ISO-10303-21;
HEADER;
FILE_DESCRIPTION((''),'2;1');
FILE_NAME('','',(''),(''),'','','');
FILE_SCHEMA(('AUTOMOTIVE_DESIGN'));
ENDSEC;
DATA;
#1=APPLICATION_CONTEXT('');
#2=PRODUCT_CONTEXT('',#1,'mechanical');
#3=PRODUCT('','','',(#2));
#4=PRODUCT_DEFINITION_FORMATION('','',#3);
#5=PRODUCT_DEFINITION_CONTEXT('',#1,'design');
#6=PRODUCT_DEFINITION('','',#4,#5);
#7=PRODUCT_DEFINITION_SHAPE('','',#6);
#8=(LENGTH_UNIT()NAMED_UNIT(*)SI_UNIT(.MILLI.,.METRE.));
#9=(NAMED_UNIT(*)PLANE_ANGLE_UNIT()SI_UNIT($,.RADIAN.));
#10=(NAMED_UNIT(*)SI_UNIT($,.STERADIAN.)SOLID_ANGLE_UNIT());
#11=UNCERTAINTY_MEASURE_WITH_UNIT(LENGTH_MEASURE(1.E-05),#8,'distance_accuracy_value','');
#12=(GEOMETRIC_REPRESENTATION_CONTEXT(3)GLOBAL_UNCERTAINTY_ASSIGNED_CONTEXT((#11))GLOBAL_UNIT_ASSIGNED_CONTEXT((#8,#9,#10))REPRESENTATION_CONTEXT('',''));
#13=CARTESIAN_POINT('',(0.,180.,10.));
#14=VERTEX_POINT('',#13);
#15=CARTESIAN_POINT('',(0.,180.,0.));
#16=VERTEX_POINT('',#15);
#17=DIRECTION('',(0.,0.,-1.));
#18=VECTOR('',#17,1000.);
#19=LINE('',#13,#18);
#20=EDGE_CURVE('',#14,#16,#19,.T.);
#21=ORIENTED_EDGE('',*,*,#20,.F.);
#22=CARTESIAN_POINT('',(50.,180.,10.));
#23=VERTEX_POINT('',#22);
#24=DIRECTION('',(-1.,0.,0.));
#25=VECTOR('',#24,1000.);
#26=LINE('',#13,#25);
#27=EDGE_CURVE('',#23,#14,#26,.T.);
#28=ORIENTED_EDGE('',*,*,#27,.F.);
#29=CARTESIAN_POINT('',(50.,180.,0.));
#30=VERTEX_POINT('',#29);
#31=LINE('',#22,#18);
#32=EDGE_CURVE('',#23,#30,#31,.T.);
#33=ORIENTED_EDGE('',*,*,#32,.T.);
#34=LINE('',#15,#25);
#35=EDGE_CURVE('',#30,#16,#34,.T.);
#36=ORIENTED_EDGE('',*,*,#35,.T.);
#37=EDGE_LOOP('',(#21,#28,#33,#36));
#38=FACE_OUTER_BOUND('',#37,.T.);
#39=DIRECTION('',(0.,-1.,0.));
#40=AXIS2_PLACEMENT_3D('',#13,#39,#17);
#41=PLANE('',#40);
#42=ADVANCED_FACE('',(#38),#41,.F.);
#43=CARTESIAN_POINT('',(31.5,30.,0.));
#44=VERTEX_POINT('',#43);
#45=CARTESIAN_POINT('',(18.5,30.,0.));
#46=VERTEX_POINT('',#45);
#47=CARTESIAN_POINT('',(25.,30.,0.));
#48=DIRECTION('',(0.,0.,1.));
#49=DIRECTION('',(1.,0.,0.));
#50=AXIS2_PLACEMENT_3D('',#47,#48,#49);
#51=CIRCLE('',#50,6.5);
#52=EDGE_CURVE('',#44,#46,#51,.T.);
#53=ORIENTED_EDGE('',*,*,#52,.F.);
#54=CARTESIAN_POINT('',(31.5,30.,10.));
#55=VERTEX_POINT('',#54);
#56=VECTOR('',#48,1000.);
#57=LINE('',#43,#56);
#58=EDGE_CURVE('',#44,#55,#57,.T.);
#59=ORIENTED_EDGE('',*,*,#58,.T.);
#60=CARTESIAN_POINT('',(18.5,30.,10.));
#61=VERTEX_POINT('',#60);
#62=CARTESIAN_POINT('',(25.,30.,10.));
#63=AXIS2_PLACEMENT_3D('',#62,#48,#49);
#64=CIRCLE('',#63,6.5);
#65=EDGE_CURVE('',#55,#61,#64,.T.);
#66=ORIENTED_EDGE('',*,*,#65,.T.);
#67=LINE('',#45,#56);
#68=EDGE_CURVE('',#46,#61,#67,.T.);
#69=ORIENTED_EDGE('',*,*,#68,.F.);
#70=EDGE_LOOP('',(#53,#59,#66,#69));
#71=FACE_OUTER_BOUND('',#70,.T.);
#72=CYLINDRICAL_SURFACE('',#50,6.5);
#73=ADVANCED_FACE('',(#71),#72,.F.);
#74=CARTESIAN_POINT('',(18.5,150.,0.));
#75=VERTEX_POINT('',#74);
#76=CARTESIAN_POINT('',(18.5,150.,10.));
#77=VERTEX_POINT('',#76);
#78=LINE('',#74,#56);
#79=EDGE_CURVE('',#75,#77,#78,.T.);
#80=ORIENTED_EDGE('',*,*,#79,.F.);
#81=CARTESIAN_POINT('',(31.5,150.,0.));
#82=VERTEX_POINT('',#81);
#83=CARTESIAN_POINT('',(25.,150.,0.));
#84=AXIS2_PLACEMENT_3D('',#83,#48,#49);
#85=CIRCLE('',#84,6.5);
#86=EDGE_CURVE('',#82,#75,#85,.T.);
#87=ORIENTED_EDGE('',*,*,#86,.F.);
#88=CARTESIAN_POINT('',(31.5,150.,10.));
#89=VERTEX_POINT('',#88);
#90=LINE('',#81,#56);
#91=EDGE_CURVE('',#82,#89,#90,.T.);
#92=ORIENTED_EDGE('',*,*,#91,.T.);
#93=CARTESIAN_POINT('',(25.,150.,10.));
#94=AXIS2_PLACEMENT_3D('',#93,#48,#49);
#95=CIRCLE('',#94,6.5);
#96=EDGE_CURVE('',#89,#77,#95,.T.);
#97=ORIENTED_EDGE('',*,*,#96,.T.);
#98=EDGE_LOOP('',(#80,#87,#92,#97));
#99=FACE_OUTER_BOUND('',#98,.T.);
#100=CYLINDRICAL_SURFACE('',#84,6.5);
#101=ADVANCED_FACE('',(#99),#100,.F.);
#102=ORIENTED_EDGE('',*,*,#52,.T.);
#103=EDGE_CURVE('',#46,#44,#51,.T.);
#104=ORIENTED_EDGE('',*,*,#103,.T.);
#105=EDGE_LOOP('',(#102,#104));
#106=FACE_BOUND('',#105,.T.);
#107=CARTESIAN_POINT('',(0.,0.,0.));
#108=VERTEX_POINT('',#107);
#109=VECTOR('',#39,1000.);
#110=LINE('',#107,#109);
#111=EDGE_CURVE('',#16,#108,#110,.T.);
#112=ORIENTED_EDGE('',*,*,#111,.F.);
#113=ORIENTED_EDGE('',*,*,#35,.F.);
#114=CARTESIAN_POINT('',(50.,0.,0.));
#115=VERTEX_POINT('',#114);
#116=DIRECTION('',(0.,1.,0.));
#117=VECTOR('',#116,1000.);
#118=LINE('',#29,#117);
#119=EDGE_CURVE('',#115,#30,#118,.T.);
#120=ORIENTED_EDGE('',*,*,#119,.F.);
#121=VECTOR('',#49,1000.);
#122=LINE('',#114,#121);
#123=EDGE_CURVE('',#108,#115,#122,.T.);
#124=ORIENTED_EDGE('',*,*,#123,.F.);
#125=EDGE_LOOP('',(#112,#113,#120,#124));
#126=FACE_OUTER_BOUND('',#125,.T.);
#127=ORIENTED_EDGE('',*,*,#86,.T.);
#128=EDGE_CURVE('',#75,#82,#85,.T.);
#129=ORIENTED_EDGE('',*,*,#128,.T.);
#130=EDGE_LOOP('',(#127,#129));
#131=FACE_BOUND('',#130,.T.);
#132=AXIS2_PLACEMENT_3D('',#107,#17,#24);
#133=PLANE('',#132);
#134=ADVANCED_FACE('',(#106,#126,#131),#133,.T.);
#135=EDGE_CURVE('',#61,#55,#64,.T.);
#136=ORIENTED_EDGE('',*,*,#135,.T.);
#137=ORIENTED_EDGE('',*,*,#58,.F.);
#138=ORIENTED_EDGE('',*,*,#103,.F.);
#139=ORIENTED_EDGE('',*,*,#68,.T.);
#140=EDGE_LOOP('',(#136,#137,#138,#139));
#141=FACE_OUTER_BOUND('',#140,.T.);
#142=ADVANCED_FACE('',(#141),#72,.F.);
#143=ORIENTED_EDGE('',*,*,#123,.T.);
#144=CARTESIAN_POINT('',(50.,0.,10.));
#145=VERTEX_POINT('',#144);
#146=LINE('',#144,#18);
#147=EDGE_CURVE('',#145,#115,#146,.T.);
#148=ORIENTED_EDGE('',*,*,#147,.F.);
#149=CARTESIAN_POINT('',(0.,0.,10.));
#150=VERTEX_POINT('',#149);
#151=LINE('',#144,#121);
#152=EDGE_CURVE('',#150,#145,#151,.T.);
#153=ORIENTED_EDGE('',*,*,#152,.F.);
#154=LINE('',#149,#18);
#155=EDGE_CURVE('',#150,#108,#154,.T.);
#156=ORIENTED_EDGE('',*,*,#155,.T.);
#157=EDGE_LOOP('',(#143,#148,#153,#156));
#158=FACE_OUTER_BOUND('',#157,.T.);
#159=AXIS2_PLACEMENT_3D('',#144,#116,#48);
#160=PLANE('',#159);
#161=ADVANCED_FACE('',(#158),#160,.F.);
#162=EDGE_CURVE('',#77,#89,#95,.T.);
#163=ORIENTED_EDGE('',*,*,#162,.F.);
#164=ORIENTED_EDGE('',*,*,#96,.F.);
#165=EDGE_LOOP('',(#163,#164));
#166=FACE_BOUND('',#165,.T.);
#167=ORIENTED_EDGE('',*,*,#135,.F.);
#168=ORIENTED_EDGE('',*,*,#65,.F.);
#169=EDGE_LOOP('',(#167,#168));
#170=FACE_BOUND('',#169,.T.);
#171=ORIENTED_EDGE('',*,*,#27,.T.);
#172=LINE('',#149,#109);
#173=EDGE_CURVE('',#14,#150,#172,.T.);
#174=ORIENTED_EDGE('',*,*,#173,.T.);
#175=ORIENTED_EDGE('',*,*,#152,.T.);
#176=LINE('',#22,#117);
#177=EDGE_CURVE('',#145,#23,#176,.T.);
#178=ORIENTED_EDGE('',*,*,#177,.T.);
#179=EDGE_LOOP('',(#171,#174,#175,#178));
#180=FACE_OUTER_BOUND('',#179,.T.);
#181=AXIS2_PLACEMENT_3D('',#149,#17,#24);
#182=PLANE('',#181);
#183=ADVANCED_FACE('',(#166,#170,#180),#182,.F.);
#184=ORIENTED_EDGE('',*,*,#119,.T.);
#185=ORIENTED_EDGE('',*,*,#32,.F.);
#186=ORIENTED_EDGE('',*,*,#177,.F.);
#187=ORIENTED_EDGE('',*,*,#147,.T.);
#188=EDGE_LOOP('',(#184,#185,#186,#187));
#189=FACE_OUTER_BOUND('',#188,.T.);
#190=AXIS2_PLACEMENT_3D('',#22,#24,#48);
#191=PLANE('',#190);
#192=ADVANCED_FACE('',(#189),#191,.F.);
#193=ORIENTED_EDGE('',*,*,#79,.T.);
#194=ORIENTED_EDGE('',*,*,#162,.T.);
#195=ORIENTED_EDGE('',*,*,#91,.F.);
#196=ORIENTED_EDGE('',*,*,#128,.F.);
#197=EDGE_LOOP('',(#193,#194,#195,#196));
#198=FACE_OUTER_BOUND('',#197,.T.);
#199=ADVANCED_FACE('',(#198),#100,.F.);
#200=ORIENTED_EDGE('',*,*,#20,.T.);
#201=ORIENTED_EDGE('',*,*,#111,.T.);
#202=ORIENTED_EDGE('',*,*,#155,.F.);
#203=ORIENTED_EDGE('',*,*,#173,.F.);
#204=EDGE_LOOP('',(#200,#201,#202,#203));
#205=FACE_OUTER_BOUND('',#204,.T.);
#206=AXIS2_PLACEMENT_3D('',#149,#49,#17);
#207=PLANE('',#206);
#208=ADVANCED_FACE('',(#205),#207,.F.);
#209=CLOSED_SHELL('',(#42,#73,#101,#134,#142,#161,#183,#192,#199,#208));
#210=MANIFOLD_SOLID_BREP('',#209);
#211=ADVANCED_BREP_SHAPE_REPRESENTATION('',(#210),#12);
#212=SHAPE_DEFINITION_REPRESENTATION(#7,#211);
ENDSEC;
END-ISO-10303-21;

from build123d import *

# Parameters (mm, degrees)
SKETCH_1_W          = 50
SKETCH_1_H          = 180
EXTRUDE_1_DEPTH     = 10
SKETCH_2_R          = 6.5
CUT_EXTRUDE_1_DEPTH = 10


with BuildPart() as part:
    # 草图1 → 凸台-拉伸1 (new body)
    with BuildSketch(Plane.XY):
        with Locations((25, 90)):
            Rectangle(SKETCH_1_W, SKETCH_1_H)
    extrude(amount=EXTRUDE_1_DEPTH)

    # 草图2 → 切除-拉伸1 (cut)
    with BuildSketch(Plane.XY.offset(10)):
        with Locations((25, 150)):
            Circle(SKETCH_2_R)
        with Locations((25, 30)):
            Circle(SKETCH_2_R)
    extrude(amount=-CUT_EXTRUDE_1_DEPTH, mode=Mode.SUBTRACT)


solid = part.part
